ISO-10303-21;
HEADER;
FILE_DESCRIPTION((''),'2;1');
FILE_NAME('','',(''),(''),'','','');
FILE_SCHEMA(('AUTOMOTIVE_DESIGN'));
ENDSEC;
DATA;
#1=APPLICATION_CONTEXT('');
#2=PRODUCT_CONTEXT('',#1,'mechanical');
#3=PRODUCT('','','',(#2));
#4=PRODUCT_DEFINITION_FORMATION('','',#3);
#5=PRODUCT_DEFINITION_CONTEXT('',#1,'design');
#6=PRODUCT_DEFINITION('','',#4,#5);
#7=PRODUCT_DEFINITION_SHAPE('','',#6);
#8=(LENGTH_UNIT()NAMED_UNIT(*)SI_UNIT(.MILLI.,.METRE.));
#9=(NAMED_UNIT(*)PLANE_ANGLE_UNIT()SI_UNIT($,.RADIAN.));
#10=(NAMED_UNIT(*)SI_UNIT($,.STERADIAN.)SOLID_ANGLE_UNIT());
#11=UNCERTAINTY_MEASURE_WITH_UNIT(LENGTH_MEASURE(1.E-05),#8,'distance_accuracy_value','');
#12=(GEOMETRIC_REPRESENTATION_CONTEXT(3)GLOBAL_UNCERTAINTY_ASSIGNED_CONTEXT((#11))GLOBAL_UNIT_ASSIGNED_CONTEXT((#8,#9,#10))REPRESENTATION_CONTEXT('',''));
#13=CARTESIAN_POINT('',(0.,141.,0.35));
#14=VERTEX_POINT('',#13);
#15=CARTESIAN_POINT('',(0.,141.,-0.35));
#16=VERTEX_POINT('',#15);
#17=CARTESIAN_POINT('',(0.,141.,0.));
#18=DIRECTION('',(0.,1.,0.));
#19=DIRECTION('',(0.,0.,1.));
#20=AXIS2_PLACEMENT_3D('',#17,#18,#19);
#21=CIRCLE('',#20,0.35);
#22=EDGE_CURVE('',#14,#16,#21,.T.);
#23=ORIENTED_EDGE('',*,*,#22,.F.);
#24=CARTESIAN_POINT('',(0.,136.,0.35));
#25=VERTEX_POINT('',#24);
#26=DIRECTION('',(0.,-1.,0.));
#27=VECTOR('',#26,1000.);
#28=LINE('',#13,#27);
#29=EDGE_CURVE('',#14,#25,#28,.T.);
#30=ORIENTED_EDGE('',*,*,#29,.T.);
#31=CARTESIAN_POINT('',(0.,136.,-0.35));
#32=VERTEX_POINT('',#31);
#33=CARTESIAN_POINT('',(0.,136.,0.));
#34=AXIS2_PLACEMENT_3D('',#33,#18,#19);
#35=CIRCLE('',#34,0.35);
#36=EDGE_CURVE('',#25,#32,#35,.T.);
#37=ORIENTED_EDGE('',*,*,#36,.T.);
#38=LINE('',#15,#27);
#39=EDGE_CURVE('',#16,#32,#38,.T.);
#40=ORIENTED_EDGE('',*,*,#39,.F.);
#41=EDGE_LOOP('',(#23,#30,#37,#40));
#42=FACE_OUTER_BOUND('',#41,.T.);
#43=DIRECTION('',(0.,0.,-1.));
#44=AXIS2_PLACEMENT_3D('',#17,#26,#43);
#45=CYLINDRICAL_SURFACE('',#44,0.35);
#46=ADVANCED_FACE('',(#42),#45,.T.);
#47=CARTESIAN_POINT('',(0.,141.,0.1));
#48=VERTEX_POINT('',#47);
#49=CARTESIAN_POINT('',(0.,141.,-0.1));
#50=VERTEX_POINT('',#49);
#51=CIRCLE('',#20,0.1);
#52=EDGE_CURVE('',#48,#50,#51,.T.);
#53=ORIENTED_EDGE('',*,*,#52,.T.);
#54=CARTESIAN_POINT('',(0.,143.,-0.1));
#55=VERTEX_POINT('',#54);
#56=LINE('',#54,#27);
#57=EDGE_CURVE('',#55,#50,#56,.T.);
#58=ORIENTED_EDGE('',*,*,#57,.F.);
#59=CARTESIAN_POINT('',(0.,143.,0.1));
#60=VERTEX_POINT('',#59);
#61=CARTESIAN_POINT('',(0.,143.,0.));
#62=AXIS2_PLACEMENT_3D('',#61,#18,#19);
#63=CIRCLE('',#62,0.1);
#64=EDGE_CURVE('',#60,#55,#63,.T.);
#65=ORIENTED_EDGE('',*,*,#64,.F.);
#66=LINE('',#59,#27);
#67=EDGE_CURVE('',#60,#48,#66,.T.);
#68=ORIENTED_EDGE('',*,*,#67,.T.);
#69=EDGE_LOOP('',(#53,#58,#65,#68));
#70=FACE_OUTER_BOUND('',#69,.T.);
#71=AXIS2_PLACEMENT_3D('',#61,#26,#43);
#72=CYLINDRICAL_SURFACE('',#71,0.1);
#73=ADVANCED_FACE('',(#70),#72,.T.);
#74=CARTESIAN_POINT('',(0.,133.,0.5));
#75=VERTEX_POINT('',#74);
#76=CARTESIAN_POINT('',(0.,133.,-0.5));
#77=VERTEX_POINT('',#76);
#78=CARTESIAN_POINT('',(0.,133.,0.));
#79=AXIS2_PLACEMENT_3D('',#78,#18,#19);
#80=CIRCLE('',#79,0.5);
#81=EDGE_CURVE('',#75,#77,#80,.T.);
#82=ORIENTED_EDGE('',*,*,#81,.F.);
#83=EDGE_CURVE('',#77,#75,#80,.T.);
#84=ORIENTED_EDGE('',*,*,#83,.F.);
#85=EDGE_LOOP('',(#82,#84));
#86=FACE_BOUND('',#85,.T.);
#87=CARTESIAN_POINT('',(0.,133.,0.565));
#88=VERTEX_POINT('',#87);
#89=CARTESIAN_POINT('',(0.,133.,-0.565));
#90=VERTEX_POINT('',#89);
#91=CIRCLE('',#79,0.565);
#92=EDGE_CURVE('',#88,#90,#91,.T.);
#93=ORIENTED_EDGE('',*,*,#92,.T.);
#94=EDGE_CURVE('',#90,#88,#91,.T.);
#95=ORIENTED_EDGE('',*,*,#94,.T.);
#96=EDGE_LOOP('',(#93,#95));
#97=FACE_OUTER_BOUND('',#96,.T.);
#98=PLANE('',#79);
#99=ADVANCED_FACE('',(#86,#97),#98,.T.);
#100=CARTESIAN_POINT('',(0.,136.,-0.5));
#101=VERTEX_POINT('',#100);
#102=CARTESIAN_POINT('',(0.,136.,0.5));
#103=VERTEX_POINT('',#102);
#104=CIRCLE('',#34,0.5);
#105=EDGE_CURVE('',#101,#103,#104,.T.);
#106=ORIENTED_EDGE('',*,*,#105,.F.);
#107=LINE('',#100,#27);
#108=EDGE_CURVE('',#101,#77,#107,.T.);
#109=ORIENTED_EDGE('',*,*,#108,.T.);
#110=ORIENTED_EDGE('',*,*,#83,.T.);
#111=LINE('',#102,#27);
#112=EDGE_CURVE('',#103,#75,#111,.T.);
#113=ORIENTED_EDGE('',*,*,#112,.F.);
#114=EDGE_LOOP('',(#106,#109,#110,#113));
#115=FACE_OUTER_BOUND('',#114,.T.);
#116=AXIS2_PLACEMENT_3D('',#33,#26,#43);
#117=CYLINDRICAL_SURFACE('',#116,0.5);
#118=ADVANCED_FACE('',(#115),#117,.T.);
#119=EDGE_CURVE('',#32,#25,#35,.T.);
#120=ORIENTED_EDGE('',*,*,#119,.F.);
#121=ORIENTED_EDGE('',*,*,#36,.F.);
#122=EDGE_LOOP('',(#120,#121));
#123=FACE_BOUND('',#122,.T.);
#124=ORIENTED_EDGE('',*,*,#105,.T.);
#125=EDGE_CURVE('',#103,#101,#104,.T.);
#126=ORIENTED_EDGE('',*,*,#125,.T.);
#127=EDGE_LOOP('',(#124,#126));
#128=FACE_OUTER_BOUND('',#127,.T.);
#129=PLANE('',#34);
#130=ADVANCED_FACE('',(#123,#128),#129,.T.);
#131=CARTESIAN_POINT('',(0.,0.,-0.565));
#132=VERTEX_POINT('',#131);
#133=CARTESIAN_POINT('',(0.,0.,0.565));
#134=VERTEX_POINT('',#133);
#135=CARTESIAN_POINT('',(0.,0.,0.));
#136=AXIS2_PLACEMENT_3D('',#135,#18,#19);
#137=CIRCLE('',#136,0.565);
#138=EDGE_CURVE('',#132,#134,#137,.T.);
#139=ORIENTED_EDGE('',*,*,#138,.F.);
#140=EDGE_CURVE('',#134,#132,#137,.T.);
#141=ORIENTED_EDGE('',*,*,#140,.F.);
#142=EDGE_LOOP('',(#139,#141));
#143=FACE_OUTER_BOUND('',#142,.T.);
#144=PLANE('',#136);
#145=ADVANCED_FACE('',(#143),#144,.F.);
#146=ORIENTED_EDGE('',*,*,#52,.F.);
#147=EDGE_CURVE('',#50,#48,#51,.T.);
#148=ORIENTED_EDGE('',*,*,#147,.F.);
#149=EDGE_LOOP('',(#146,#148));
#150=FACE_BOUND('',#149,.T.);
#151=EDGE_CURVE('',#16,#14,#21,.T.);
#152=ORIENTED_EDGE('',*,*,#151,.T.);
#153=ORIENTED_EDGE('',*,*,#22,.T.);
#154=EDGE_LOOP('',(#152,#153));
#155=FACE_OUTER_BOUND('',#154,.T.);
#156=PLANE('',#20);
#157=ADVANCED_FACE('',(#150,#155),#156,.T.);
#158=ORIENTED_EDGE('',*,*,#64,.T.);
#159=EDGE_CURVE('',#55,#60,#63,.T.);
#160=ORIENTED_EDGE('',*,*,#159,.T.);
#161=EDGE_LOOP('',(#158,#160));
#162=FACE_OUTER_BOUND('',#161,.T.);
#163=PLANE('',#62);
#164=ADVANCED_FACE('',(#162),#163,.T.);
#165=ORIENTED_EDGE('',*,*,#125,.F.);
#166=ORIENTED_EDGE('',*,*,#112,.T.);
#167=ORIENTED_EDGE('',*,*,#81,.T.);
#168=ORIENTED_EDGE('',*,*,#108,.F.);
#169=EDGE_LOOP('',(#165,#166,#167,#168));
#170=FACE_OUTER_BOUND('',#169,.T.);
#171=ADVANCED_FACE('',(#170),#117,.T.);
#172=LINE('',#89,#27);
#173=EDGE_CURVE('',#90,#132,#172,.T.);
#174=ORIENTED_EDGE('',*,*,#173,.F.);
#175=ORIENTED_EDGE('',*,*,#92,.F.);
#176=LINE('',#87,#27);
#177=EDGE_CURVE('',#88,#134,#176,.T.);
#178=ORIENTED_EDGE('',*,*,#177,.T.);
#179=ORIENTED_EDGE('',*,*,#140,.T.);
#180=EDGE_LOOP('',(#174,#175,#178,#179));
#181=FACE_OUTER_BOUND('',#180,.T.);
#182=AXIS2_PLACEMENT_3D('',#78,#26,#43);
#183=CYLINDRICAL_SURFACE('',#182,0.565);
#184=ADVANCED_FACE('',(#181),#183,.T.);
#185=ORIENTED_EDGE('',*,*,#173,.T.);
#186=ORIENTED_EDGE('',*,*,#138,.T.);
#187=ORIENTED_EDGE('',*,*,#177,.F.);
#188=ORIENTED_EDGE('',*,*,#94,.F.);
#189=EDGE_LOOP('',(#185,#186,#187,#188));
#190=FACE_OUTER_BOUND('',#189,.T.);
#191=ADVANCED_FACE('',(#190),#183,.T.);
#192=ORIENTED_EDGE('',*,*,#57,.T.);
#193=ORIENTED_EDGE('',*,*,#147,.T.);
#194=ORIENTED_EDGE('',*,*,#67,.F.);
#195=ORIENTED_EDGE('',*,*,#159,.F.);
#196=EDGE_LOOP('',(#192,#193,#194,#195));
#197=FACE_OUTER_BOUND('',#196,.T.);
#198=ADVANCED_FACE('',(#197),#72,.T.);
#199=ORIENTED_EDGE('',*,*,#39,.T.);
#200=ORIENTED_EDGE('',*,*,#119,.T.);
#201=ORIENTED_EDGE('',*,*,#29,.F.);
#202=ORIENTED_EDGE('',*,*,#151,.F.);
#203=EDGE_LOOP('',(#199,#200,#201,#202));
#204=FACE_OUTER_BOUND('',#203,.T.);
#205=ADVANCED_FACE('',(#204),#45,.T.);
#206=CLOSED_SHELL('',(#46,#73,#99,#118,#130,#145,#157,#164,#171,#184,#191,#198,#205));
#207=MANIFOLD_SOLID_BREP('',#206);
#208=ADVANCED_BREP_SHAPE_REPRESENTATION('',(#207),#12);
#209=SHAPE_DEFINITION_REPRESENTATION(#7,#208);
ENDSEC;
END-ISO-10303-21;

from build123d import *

# Parameters (mm, degrees)
SKETCH_1_R      = 0.565
EXTRUDE_1_DEPTH = 133
SKETCH_2_R      = 0.5
EXTRUDE_2_DEPTH = 3
SKETCH_3_R      = 0.35
EXTRUDE_3_DEPTH = 5
SKETCH_5_R      = 0.1
EXTRUDE_4_DEPTH = 2


with BuildPart() as part:
    # 草图1 → 凸台-拉伸1 (new body)
    with BuildSketch(Plane(origin=(0, 0, 0), x_dir=(1, 0, 0), z_dir=(0, 1, 0))):
        with Locations(Location((0, 0, 0), (0, 0, 270))):
            Circle(SKETCH_1_R)
    extrude(amount=EXTRUDE_1_DEPTH)

    # 草图2 → 凸台-拉伸2 (add)
    with BuildSketch(Plane(origin=(0, 133, 0), x_dir=(1, 0, 0), z_dir=(0, 1, 0))):
        with Locations(Location((0, 0, 0), (0, 0, 270))):
            Circle(SKETCH_2_R)
    extrude(amount=EXTRUDE_2_DEPTH)

    # 草图3 → 凸台-拉伸3 (add)
    with BuildSketch(Plane(origin=(0, 136, 0), x_dir=(1, 0, 0), z_dir=(0, 1, 0))):
        with Locations(Location((0, 0, 0), (0, 0, 270))):
            Circle(SKETCH_3_R)
    extrude(amount=EXTRUDE_3_DEPTH)

    # 草图5 → 凸台-拉伸4 (add)
    with BuildSketch(Plane(origin=(0, 141, 0), x_dir=(1, 0, 0), z_dir=(0, 1, 0))):
        with Locations(Location((0, 0, 0), (0, 0, 270))):
            Circle(SKETCH_5_R)
    extrude(amount=EXTRUDE_4_DEPTH)


solid = part.part
